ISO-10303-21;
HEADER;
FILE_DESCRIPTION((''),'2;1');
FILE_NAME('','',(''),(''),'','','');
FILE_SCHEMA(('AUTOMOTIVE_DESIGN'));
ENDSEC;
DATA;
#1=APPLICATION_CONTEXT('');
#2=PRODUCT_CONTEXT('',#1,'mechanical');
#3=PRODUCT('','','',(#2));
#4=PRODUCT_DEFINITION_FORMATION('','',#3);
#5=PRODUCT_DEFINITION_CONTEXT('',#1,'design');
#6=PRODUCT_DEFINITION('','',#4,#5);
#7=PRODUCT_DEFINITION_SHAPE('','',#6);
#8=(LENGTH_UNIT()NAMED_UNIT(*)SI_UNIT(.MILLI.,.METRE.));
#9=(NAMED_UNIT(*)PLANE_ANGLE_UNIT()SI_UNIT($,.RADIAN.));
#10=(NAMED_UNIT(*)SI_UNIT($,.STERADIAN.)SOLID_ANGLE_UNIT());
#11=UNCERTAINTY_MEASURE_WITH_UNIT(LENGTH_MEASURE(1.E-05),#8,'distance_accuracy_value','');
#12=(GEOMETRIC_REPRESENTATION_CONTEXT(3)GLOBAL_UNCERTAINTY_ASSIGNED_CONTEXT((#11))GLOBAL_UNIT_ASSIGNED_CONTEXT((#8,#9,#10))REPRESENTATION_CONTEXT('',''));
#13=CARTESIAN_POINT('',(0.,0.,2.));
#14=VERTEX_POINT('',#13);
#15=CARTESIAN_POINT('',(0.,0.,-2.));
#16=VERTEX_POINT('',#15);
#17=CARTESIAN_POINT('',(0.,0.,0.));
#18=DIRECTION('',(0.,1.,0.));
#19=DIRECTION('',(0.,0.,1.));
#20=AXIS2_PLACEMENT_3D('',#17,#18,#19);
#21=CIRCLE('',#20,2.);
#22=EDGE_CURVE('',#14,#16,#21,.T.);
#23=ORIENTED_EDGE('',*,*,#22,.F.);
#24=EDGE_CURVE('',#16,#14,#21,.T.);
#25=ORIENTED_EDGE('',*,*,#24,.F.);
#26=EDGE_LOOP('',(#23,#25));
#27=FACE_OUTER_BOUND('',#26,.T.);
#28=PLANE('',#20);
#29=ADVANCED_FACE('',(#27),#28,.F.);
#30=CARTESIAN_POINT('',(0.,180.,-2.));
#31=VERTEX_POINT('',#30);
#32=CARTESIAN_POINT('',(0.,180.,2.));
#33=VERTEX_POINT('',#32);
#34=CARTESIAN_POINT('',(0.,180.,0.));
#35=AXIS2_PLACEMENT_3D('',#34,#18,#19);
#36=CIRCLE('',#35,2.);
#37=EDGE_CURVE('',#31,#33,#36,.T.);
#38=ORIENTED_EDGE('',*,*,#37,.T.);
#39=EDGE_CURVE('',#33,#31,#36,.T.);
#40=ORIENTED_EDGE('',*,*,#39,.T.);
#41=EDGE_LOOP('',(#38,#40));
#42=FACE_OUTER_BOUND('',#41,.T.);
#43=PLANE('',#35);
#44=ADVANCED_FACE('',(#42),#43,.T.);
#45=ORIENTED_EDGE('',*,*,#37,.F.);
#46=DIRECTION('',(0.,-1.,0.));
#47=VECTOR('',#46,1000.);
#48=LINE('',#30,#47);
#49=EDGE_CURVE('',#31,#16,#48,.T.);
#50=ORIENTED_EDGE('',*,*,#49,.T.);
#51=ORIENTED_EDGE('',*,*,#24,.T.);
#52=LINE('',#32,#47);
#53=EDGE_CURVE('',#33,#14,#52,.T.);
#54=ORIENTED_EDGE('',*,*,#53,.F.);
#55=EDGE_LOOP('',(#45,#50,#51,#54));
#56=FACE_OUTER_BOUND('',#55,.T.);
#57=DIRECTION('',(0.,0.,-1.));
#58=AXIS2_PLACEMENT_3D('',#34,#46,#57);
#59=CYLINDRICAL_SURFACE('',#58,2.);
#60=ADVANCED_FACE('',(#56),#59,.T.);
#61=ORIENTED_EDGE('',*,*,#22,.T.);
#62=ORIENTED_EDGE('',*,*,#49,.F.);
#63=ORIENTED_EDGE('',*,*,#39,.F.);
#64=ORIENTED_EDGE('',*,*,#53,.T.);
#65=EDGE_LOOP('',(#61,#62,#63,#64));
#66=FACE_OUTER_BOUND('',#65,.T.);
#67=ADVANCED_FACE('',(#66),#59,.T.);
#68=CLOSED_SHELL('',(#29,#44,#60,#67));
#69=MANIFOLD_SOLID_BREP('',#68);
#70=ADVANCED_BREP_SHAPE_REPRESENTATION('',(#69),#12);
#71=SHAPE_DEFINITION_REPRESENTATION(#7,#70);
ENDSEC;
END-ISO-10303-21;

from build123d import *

# Parameters (mm, degrees)
SKETCH_1_R      = 2
EXTRUDE_1_DEPTH = 180


with BuildPart() as part:
    # 草图1 → 凸台-拉伸1 (new body)
    with BuildSketch(Plane(origin=(0, 0, 0), x_dir=(1, 0, 0), z_dir=(0, 1, 0))):
        with Locations(Location((0, 0, 0), (0, 0, 90))):
            Circle(SKETCH_1_R)
    extrude(amount=EXTRUDE_1_DEPTH)


solid = part.part
